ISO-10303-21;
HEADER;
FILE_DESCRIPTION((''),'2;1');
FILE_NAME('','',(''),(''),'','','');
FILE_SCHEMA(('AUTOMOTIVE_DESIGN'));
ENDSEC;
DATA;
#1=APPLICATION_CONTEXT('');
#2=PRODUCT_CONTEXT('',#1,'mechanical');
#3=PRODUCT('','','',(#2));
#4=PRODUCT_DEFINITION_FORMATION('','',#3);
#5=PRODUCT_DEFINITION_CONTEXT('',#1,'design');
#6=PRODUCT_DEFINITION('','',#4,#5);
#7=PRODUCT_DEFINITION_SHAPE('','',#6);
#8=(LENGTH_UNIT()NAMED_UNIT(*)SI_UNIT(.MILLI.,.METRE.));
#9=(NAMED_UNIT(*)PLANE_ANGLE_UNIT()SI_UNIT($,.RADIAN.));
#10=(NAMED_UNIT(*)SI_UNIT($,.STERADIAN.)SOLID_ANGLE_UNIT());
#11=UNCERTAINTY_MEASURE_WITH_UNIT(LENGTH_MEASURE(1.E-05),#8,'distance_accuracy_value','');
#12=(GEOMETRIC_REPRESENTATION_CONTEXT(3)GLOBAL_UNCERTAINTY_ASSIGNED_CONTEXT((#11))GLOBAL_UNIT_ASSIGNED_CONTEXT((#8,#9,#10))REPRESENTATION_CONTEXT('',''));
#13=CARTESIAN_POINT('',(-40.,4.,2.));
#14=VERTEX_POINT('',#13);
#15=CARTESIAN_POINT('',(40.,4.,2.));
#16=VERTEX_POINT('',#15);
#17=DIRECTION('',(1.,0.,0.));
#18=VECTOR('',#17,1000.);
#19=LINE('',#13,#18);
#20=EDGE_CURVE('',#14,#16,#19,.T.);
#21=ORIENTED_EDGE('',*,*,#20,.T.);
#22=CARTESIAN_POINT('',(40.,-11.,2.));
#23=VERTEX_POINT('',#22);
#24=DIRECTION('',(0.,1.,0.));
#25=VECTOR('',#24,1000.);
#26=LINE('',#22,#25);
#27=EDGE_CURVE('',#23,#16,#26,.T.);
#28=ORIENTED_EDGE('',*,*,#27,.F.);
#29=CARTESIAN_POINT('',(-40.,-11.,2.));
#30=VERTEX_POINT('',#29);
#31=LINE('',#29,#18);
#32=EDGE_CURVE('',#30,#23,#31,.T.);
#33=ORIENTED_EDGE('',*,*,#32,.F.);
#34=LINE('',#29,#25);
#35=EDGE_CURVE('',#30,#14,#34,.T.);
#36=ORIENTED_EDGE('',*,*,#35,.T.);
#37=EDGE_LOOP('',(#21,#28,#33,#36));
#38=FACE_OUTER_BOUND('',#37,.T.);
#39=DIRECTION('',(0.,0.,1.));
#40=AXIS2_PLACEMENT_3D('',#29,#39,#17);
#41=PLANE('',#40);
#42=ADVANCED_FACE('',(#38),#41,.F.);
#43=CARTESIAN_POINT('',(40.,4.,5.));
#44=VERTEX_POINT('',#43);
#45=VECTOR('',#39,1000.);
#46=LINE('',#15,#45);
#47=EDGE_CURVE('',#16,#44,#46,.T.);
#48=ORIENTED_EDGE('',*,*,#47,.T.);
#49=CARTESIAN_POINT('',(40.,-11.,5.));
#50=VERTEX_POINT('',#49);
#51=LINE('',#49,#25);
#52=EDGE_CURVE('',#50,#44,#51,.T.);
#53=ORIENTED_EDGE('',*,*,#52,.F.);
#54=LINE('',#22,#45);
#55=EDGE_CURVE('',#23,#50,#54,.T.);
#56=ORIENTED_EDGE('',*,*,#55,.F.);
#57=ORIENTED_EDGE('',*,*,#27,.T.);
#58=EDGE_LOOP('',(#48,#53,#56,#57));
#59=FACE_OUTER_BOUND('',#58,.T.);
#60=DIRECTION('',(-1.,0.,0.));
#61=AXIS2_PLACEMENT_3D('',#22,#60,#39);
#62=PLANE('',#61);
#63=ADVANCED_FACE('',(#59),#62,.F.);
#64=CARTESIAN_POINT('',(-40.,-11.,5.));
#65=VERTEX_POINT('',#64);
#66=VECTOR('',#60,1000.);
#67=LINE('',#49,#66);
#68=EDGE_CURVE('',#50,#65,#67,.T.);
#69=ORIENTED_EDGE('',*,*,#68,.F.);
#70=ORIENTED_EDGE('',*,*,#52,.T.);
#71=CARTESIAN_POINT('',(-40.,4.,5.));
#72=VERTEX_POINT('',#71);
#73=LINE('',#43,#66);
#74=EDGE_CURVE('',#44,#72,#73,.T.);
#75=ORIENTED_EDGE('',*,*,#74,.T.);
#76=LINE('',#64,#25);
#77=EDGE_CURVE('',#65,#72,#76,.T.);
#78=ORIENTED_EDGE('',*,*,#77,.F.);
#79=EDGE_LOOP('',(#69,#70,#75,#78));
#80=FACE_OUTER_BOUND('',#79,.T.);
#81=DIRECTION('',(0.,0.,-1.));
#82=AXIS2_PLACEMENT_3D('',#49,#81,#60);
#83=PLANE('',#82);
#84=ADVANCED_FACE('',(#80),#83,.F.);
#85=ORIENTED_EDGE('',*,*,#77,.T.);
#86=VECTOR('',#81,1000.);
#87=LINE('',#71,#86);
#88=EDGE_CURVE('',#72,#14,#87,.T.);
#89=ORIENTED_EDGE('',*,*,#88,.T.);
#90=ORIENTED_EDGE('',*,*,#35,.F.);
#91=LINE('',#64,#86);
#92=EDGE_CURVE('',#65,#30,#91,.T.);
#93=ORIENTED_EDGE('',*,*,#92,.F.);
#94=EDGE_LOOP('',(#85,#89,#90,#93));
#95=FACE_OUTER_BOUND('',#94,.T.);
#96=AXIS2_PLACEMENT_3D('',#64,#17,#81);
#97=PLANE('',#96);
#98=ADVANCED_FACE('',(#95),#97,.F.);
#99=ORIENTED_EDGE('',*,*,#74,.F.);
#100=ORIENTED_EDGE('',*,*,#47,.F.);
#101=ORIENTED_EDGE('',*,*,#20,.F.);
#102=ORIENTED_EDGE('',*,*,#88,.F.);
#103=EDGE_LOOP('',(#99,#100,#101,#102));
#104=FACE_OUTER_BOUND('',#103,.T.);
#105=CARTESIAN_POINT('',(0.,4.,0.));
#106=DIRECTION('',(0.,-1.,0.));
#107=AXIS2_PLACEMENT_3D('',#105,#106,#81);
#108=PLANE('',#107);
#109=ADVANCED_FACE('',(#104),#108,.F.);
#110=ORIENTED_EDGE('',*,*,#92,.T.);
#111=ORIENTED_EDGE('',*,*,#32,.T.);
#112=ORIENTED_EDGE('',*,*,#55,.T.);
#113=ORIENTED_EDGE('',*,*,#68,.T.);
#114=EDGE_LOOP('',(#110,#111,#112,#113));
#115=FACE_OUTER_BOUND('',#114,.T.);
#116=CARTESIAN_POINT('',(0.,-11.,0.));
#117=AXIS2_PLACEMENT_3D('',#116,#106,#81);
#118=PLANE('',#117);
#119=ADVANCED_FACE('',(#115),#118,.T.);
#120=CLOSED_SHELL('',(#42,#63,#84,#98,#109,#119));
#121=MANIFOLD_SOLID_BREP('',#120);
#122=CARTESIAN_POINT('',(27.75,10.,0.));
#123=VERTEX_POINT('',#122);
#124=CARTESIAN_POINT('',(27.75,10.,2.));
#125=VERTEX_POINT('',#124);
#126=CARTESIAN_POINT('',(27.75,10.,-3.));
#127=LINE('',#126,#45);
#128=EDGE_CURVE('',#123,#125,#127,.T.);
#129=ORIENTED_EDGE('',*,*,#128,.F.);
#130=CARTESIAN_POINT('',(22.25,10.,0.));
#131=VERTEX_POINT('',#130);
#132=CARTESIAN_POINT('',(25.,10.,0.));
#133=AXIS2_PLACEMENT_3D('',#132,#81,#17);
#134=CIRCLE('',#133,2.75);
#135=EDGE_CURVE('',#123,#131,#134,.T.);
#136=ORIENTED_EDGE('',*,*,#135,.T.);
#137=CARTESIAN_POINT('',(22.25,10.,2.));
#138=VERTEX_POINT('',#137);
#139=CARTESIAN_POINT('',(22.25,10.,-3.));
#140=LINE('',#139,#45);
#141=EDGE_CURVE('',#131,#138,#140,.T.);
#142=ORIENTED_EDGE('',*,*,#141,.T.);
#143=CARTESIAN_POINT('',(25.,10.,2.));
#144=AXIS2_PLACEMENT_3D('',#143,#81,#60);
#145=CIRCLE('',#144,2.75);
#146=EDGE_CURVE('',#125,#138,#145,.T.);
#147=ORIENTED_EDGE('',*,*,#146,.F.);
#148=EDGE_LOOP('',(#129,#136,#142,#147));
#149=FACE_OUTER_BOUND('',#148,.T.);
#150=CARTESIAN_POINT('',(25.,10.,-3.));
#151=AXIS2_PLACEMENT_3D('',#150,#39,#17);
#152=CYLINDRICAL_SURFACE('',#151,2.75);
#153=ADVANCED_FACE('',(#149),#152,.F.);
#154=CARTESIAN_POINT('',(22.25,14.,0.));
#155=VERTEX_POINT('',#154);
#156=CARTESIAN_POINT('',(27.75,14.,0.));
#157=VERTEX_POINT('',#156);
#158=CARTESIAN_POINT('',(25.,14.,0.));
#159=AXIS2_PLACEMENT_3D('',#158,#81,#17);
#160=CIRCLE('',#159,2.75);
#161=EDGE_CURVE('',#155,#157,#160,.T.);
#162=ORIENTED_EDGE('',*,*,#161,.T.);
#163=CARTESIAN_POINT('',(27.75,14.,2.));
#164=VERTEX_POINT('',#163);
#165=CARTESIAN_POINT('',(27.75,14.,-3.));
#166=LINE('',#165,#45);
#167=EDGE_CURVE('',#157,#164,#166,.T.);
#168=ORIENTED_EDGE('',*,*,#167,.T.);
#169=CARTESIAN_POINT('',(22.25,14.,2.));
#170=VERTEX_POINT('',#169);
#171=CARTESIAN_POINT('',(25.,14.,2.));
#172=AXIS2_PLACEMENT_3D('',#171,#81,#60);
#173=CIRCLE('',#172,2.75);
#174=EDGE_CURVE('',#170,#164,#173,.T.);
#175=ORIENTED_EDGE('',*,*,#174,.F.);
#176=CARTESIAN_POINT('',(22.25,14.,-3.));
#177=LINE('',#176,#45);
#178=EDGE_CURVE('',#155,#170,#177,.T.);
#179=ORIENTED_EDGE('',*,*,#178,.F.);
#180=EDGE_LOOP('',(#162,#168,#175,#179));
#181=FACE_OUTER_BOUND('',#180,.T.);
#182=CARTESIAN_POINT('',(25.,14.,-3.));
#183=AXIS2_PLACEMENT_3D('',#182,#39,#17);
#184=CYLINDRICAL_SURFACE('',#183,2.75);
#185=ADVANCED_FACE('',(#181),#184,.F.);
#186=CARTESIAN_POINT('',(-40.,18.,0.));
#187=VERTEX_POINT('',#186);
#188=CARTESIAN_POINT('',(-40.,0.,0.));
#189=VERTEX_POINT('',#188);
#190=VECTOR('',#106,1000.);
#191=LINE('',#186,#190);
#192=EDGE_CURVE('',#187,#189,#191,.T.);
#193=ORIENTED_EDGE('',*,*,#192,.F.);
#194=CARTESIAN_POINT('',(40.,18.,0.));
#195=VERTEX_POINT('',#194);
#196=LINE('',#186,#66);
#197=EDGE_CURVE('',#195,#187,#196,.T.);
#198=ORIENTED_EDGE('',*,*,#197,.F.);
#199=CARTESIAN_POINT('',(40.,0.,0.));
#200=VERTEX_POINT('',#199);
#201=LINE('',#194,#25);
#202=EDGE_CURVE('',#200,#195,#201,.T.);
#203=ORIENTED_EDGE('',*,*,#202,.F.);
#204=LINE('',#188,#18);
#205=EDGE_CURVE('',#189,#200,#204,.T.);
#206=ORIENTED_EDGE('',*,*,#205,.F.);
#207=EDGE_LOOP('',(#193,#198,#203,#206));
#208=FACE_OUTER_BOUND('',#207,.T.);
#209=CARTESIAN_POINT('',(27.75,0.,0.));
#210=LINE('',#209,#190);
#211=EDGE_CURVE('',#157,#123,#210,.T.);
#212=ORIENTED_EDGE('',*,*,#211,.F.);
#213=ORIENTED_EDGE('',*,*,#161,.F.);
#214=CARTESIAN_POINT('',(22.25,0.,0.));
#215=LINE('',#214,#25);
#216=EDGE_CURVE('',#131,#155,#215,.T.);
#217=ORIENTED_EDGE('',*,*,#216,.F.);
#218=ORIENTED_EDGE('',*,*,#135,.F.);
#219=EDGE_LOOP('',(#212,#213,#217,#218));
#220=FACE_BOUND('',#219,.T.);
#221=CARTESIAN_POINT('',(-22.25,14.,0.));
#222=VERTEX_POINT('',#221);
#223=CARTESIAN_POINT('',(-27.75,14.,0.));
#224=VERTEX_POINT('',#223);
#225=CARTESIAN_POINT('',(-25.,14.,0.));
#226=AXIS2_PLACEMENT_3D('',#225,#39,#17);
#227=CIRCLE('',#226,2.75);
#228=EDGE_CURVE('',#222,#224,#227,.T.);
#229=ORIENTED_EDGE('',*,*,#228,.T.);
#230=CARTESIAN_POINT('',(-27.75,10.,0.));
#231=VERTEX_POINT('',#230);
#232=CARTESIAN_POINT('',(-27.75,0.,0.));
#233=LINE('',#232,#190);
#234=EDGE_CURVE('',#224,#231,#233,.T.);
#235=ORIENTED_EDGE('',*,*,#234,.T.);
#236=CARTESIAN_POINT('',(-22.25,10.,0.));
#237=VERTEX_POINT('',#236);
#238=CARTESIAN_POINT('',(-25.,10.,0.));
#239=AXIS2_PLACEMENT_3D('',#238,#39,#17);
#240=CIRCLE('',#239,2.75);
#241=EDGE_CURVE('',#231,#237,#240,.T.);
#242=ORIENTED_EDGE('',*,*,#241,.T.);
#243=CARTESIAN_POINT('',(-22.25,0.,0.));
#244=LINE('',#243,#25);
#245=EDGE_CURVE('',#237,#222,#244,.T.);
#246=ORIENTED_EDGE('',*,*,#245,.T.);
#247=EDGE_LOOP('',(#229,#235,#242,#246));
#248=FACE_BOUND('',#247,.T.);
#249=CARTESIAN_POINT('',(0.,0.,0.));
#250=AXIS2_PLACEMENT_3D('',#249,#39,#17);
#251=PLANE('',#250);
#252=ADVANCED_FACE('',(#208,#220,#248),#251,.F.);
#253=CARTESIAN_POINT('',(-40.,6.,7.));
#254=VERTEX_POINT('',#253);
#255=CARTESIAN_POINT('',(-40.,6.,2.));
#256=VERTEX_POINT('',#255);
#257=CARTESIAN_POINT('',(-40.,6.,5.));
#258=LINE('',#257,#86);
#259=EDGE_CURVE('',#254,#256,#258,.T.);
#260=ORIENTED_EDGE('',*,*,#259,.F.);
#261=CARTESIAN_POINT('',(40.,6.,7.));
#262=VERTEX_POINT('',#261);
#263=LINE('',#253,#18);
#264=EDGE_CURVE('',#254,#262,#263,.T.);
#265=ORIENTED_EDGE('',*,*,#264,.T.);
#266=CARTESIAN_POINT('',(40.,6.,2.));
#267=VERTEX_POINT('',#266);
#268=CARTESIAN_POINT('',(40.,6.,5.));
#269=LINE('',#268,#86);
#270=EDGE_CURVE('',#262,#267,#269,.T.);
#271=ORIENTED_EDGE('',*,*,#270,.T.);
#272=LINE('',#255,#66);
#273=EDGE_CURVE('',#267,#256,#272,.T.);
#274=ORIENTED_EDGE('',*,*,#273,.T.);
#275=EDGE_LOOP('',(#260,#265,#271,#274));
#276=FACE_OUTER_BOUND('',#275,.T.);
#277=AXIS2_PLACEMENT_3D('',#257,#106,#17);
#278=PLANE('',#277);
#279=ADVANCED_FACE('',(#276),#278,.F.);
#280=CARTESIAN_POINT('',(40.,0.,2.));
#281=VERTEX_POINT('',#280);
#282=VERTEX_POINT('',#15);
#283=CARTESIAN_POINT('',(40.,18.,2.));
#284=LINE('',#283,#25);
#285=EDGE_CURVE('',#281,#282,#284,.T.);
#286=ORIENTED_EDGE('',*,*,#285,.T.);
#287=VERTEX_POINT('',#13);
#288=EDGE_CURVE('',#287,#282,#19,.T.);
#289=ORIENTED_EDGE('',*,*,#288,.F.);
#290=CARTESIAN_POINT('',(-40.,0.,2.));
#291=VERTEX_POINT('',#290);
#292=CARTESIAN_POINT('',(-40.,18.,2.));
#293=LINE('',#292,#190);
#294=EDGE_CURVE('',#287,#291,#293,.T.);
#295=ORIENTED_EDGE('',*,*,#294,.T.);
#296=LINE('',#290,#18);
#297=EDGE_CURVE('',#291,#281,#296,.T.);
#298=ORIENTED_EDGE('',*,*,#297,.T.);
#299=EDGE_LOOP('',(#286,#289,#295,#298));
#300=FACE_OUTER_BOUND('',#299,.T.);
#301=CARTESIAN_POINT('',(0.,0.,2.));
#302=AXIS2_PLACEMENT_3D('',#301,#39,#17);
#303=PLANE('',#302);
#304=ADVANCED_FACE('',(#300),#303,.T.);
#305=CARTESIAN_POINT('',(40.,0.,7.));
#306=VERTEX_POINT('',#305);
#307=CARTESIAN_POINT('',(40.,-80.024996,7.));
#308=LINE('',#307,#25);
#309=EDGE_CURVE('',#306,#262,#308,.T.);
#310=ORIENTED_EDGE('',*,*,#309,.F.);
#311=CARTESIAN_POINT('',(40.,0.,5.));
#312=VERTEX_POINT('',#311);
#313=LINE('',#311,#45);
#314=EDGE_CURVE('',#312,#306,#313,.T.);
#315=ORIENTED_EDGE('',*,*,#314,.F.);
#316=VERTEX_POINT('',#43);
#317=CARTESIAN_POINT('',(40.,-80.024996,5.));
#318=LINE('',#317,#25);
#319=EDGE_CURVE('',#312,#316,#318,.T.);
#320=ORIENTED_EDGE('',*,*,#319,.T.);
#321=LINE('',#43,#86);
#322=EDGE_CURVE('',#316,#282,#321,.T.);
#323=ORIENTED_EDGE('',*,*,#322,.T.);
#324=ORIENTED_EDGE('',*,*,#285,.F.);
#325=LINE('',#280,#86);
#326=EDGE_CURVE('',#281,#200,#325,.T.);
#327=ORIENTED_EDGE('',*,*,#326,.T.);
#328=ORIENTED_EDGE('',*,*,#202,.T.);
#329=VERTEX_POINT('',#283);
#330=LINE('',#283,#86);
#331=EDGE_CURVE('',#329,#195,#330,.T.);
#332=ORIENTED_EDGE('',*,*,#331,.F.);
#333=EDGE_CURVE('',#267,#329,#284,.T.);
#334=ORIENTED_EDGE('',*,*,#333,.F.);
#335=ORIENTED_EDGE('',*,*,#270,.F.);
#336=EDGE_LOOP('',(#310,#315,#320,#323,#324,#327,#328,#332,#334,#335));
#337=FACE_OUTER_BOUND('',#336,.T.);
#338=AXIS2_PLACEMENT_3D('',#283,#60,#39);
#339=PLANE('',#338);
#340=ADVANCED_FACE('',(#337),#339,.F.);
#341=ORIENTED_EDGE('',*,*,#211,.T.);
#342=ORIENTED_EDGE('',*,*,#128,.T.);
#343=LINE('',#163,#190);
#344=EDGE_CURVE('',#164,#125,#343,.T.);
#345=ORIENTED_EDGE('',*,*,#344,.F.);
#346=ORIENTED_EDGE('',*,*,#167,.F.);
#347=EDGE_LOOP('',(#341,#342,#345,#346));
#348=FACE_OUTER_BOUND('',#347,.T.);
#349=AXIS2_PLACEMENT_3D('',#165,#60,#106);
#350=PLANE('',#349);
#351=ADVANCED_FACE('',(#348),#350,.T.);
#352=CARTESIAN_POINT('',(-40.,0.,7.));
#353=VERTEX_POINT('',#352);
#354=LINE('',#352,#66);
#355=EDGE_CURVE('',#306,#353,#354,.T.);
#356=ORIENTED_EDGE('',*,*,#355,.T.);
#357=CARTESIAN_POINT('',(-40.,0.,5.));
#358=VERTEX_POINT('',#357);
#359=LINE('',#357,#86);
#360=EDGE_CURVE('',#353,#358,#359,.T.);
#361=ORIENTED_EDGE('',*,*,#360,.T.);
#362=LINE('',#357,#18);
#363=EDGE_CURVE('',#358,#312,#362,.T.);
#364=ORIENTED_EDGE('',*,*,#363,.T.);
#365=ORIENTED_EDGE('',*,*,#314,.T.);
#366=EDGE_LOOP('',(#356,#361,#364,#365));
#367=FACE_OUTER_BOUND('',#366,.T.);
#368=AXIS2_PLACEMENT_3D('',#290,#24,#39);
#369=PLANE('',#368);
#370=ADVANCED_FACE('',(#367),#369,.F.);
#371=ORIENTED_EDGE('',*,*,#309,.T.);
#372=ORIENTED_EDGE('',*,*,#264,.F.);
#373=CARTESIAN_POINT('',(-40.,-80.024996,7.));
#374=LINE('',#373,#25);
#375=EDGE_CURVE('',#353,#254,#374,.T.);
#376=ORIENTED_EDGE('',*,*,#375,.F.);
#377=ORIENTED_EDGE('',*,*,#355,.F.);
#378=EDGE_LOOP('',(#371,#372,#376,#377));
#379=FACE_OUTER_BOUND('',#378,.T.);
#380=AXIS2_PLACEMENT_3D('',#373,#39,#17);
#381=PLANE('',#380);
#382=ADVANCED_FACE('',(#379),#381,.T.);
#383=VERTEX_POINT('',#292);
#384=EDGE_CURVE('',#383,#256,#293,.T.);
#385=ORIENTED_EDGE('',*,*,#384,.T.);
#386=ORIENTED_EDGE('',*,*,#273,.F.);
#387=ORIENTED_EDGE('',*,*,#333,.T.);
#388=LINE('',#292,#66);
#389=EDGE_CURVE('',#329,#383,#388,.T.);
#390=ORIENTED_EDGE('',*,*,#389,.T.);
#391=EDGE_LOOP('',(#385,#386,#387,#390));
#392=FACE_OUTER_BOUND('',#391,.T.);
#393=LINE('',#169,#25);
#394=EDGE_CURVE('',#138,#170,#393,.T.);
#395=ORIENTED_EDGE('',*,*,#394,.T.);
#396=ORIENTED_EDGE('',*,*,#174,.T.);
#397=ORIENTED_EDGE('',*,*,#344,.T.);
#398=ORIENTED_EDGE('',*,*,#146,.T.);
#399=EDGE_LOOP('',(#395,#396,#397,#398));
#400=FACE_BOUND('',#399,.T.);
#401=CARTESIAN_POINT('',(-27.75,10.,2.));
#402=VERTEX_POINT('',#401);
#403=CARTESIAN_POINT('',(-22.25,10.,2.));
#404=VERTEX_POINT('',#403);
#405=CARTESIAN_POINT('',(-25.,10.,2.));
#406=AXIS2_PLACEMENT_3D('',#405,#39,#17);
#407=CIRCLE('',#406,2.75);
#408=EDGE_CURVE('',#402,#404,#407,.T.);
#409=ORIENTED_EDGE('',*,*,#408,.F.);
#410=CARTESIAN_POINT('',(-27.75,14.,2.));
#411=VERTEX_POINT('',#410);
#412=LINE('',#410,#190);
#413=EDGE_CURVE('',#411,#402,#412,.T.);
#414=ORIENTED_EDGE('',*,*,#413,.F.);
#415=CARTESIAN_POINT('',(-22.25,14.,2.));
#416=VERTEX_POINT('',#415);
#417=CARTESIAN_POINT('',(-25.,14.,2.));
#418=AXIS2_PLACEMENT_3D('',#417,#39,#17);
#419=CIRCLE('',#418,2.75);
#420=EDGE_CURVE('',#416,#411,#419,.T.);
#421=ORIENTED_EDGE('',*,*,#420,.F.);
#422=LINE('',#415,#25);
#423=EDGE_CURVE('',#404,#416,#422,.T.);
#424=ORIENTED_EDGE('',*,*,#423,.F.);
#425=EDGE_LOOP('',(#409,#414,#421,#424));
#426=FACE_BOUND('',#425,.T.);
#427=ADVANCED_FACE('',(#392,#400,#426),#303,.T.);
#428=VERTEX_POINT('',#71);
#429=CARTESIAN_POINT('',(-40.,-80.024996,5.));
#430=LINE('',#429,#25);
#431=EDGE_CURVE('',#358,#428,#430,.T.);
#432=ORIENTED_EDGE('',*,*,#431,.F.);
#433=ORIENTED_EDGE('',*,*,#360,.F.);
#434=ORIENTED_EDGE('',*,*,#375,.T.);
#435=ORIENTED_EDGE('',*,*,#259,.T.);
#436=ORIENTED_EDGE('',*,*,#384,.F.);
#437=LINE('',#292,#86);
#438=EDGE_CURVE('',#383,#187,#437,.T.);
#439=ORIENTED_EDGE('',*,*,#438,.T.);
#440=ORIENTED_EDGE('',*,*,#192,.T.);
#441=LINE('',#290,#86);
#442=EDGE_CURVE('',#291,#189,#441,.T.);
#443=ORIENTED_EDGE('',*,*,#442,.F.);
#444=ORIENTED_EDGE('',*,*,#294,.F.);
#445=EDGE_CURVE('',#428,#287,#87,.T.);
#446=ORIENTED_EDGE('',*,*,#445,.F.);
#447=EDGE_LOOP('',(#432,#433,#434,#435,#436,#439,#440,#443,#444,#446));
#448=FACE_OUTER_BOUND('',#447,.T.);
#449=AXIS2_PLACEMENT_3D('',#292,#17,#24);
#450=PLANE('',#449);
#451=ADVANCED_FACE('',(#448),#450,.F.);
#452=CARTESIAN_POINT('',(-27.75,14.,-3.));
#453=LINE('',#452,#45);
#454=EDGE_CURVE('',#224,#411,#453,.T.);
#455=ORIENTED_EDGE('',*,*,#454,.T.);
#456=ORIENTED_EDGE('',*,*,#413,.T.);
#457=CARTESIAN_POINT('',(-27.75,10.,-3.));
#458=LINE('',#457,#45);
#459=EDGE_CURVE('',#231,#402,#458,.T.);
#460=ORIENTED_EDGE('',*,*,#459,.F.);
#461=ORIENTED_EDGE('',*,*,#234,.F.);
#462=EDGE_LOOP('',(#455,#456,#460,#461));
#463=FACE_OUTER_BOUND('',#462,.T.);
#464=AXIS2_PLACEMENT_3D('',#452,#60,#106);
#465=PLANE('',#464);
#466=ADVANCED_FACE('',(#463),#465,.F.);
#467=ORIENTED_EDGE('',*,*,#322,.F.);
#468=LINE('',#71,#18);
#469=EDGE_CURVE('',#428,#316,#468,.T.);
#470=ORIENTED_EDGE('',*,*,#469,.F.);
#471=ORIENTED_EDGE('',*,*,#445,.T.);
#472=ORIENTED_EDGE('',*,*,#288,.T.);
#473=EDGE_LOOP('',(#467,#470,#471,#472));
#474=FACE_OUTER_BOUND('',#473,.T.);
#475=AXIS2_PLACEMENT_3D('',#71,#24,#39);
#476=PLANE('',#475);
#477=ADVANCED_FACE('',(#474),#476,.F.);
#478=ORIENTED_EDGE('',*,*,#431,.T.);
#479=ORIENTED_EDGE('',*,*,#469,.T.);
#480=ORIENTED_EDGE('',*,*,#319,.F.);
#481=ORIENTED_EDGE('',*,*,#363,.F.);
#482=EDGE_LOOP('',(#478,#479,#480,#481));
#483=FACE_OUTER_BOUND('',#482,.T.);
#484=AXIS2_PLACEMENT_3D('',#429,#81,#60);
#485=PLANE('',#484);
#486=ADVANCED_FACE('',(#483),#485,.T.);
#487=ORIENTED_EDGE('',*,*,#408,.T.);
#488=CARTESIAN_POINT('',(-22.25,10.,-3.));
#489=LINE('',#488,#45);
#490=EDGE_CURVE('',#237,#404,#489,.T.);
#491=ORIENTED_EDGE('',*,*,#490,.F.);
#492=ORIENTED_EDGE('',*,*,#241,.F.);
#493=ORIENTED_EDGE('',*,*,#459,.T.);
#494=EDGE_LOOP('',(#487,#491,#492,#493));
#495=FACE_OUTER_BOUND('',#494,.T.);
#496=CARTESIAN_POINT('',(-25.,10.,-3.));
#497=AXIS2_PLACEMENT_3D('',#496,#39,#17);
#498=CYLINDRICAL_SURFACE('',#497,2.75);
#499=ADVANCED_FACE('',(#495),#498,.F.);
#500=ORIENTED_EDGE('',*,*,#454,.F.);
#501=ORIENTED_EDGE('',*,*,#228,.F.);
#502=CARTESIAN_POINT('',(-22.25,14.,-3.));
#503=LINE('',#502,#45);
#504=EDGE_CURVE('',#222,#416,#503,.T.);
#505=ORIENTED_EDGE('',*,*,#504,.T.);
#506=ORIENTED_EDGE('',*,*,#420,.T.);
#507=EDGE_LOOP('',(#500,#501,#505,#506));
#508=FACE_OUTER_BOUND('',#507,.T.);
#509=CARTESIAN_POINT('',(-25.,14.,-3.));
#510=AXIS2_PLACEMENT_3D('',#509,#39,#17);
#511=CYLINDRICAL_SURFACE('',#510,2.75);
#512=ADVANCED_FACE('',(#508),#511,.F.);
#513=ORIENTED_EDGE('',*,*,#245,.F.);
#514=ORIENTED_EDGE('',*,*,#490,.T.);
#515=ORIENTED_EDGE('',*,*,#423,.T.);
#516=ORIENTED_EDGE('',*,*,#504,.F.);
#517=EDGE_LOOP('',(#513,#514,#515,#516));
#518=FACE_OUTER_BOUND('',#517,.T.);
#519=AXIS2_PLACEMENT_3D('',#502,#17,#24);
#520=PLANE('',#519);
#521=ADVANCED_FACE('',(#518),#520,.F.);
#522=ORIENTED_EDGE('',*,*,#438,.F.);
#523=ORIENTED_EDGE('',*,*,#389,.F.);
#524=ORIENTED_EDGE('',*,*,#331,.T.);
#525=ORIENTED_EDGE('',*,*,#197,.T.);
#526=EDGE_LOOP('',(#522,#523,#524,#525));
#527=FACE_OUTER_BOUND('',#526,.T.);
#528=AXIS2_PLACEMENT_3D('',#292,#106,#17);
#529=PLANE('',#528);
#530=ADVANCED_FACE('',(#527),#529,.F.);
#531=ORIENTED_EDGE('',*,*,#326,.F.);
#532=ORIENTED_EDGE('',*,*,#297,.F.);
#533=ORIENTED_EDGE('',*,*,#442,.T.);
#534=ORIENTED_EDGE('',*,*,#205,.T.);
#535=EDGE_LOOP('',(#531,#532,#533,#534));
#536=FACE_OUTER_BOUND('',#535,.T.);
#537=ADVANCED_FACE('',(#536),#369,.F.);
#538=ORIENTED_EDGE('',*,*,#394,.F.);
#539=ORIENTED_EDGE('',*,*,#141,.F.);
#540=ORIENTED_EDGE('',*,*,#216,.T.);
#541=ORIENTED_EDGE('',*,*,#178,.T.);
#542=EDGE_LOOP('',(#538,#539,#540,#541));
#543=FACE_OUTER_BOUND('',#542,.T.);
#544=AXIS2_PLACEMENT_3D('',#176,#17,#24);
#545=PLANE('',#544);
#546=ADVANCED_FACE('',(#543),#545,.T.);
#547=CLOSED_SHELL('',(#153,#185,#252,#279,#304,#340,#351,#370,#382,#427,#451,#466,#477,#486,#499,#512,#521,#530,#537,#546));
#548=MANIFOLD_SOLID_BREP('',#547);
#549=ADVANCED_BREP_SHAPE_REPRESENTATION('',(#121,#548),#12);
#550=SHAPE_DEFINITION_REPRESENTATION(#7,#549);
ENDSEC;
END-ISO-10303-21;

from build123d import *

# Parameters (mm, degrees)
SKETCH_1_W          = 80
SKETCH_1_H          = 18
EXTRUDE_1_DEPTH     = 2
SKETCH_2_W          = 80
SKETCH_2_H          = 2
EXTRUDE_2_DEPTH     = 3
SKETCH_3_W          = 80
SKETCH_3_H          = 2
EXTRUDE_3_DEPTH     = 6
SKETCH_5_W          = 80
SKETCH_5_H          = 3
EXTRUDE_5_DEPTH     = 15
CUT_EXTRUDE_1_DEPTH = 5


with BuildPart() as part:
    # 草图1 → 凸台-拉伸1 (new body)
    with BuildSketch(Plane.XY):
        with Locations((0, 9)):
            Rectangle(SKETCH_1_W, SKETCH_1_H)
    extrude(amount=EXTRUDE_1_DEPTH)

    # 草图2 → 凸台-拉伸2 (add)
    with BuildSketch(Plane.XY.offset(2)):
        with Locations((0, 5)):
            Rectangle(SKETCH_2_W, SKETCH_2_H)
    extrude(amount=EXTRUDE_2_DEPTH)

    # 草图3 → 凸台-拉伸3 (add)
    with BuildSketch(Plane(origin=(0, 6, 0), x_dir=(1, 0, 0), z_dir=(0, 1, 0))):
        with Locations((0, -6)):
            Rectangle(SKETCH_3_W, SKETCH_3_H)
    extrude(amount=-EXTRUDE_3_DEPTH)

    # 草图6 → 切除-拉伸1 (cut)
    with BuildSketch(Plane.XY.offset(2)):
        with BuildLine():
            Line((-22.25, 14), (-22.25, 10))
            ThreePointArc((-22.25, 10), (-25, 7.25), (-27.75, 10))
            Line((-27.75, 10), (-27.75, 14))
            ThreePointArc((-27.75, 14), (-25, 16.75), (-22.25, 14))
        make_face()
    cut_extrude_1 = extrude(amount=-CUT_EXTRUDE_1_DEPTH, mode=Mode.SUBTRACT)

    # 镜向1: 切除-拉伸1 across plane
    add(cut_extrude_1.mirror(Plane.ZY), mode=Mode.SUBTRACT)


with BuildPart() as body_2:
    # 草图5 → 凸台-拉伸5 (new body)
    with BuildSketch(Plane.XZ.offset(-4)):
        with Locations((0, 3.5)):
            Rectangle(SKETCH_5_W, SKETCH_5_H)
    extrude(amount=EXTRUDE_5_DEPTH)


solid = Compound([part.part, body_2.part])
